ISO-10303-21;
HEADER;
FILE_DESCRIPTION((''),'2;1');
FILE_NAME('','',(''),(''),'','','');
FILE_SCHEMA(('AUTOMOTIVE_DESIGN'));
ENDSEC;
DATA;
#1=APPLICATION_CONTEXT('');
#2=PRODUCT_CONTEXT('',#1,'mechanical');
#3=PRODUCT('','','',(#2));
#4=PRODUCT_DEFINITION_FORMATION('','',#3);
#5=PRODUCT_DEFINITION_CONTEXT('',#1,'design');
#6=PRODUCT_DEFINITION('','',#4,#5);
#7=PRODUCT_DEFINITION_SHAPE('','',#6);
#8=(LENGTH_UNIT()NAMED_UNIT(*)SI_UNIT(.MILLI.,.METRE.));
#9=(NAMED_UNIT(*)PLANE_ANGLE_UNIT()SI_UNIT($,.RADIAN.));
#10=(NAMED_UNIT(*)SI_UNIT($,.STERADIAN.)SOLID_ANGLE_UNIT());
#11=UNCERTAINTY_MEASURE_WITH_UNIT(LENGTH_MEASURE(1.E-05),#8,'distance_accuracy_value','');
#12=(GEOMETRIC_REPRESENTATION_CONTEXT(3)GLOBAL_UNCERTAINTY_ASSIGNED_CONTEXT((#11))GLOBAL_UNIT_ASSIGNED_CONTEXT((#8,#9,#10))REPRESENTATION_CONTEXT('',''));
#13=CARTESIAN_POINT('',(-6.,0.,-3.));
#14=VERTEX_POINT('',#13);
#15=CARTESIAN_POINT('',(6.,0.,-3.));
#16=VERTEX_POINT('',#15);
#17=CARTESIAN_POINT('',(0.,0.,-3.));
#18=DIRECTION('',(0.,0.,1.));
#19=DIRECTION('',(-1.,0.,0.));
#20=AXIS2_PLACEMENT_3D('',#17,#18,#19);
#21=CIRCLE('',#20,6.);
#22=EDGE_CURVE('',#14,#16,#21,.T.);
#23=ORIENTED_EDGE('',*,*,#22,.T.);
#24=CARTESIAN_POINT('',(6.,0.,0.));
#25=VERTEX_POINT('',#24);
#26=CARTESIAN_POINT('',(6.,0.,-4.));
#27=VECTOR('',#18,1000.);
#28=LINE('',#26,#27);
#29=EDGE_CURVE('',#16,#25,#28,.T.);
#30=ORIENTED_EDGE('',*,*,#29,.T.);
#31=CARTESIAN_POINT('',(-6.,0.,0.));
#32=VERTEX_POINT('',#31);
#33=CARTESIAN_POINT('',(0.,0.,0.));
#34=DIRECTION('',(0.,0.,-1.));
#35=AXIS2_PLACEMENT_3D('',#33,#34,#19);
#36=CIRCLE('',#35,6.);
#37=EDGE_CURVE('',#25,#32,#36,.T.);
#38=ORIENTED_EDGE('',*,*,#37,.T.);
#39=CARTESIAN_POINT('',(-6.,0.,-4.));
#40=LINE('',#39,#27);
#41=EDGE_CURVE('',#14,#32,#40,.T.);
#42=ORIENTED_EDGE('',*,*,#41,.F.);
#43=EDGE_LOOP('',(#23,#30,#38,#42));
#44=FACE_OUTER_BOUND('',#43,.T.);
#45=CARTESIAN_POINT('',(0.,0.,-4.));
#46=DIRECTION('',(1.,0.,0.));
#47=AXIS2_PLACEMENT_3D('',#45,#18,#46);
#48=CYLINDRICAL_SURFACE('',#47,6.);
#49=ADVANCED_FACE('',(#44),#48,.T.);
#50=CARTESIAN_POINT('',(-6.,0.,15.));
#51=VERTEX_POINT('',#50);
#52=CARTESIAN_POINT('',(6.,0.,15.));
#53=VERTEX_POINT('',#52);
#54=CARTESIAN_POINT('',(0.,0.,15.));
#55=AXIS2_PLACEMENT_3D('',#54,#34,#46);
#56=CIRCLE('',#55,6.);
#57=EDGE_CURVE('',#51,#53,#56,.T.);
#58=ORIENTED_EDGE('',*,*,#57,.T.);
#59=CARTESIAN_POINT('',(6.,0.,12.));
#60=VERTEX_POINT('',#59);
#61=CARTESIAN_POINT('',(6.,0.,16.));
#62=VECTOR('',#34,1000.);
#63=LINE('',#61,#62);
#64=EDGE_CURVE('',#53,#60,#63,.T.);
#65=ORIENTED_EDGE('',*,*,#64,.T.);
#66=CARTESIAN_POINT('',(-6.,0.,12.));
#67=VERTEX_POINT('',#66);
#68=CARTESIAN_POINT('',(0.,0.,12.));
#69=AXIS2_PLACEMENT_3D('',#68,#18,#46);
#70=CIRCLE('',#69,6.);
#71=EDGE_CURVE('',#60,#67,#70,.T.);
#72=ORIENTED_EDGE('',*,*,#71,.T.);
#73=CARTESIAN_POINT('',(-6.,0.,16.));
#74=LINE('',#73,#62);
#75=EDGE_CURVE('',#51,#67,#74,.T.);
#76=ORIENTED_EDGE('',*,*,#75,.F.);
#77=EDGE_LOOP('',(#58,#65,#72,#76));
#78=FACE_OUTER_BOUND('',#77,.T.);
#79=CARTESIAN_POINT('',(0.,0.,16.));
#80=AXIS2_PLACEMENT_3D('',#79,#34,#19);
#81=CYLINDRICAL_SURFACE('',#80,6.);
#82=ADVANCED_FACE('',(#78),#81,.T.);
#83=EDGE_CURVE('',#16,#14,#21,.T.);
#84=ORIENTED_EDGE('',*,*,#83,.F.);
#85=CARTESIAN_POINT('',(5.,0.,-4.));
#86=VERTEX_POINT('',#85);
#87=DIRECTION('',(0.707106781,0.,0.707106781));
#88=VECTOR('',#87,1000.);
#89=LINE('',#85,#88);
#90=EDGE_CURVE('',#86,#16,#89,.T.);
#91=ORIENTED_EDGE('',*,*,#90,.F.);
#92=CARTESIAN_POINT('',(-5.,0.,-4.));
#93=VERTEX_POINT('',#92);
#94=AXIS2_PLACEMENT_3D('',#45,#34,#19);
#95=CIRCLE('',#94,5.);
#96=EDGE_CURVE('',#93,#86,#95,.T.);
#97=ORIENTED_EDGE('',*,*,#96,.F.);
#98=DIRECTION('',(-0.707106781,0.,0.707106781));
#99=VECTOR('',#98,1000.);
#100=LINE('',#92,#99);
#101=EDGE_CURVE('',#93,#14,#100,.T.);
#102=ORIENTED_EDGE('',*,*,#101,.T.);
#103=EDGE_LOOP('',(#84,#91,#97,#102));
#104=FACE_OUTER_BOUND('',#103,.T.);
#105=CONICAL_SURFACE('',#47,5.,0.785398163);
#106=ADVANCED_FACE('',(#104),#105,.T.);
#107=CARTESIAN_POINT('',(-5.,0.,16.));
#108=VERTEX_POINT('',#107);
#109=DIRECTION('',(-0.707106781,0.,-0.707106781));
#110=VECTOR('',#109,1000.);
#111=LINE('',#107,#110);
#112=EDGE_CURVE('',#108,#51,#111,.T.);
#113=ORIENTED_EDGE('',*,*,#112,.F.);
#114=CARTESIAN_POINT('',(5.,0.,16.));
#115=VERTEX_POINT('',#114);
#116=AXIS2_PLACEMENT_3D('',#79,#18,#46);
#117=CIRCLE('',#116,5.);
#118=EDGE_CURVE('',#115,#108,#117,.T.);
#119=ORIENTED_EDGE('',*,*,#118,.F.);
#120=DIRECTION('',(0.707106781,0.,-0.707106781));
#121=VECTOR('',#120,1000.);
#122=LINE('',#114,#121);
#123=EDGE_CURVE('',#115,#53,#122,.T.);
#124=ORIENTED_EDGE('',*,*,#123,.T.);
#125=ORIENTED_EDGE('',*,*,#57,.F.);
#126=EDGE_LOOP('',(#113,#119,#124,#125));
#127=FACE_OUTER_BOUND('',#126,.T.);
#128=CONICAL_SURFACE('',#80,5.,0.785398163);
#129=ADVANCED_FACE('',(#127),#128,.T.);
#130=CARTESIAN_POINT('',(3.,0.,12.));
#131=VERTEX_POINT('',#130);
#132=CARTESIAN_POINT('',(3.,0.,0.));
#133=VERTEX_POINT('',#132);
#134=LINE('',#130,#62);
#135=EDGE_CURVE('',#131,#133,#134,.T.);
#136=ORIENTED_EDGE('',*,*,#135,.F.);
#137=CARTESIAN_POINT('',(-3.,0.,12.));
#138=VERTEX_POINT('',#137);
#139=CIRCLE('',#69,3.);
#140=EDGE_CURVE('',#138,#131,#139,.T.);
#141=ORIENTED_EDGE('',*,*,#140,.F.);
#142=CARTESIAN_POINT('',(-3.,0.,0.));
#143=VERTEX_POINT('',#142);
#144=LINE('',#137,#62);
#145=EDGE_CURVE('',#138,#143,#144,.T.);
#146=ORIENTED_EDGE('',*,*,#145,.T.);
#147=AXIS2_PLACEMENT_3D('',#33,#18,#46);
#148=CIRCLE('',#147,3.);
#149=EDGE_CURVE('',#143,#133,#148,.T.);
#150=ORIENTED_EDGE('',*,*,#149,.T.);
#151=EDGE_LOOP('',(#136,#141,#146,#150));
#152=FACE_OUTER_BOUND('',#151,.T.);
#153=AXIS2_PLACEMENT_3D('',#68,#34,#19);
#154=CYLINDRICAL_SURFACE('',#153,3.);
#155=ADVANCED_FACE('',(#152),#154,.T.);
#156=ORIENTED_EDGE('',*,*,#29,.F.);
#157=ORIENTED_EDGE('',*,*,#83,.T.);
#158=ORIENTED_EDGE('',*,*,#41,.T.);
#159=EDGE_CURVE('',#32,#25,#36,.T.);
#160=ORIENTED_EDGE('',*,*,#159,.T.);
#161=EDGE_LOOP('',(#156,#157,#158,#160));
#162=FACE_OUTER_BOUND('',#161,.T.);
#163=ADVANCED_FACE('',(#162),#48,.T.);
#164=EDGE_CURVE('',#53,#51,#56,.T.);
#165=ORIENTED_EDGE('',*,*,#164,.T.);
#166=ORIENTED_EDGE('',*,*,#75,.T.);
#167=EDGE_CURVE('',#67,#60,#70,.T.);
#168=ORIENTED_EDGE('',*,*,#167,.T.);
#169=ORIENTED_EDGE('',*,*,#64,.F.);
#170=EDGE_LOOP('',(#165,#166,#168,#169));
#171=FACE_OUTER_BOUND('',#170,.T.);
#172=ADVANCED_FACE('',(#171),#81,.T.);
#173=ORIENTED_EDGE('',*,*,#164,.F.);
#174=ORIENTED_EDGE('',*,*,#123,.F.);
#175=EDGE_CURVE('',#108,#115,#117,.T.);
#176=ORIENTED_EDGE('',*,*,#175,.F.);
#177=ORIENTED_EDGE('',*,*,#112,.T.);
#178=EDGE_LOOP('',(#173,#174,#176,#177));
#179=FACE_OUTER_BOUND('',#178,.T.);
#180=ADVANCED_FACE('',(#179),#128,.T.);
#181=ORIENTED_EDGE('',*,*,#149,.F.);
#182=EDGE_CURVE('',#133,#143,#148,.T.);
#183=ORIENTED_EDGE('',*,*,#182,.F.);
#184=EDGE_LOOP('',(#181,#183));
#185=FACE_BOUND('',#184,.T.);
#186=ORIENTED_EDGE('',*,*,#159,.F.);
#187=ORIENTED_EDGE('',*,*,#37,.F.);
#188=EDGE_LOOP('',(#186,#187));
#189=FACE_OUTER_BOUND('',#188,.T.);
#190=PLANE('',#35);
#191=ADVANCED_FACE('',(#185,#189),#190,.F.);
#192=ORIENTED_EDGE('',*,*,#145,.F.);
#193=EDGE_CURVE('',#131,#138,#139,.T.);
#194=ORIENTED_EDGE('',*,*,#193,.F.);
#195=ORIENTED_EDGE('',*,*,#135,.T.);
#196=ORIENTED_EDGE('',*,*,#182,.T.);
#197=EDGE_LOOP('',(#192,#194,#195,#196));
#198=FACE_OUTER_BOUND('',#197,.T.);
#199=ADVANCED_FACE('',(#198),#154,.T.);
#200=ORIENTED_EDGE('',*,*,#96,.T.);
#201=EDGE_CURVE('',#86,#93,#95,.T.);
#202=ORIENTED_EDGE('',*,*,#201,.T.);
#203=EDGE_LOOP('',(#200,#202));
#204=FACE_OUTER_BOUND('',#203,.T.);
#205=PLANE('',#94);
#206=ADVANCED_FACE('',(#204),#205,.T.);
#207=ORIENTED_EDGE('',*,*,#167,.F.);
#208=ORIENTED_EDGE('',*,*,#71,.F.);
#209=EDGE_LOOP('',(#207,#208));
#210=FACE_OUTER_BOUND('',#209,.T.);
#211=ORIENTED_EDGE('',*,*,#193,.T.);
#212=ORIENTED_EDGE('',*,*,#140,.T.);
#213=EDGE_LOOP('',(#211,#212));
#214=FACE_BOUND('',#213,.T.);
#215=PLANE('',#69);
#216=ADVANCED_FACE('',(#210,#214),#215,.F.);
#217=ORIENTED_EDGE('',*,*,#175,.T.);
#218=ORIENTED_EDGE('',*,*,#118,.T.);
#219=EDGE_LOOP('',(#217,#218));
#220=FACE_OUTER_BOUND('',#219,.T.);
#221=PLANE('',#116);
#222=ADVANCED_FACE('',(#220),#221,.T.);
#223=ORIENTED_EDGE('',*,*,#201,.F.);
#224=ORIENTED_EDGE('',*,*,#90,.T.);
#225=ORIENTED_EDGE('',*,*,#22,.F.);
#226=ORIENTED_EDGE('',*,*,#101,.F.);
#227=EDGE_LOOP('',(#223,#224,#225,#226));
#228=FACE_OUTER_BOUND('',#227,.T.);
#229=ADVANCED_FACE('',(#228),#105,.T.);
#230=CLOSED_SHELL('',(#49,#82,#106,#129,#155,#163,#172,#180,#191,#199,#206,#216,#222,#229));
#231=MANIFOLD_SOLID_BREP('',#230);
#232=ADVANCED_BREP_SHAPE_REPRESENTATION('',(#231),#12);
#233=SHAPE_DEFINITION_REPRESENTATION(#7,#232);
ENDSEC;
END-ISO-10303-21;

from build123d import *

# Parameters (mm, degrees)
SKETCH_1_R      = 3
EXTRUDE_1_DEPTH = 12
SKETCH_2_R      = 6
EXTRUDE_2_DEPTH = 4
CHAMFER_1_SIZE  = 1
EXTRUDE_START   = 4
SKETCH_3_R      = 6
EXTRUDE_3_DEPTH = 4
CHAMFER_2_SIZE  = 1


with BuildPart() as part:
    # 草图1 → 凸台-拉伸1 (new body)
    with BuildSketch(Plane.XY):
        Circle(SKETCH_1_R)
    extrude(amount=EXTRUDE_1_DEPTH)

    # 草图2 → 凸台-拉伸2 (add)
    with BuildSketch(Plane.XY.offset(12)):
        Circle(SKETCH_2_R)
    extrude(amount=EXTRUDE_2_DEPTH)

    # 倒角1
    chamfer_1_edges = [part.edges().sort_by_distance(p)[0] for p in [
        (-6, 0, 16),
    ]]
    chamfer(chamfer_1_edges, length=CHAMFER_1_SIZE)

    # 草图3 → 凸台-拉伸3 (add)
    with BuildSketch(Plane(origin=(0, 0, 0), x_dir=(-1, 0, 0), z_dir=(0, 0, -1)).offset(EXTRUDE_START)):
        with Locations(Location((0, 0, 0), (0, 0, 180))):
            Circle(SKETCH_3_R)
    extrude(amount=-EXTRUDE_3_DEPTH)

    # 倒角2
    chamfer_2_edges = [part.edges().sort_by_distance(p)[0] for p in [
        (-6, 0, -4),
    ]]
    chamfer(chamfer_2_edges, length=CHAMFER_2_SIZE)


solid = part.part
